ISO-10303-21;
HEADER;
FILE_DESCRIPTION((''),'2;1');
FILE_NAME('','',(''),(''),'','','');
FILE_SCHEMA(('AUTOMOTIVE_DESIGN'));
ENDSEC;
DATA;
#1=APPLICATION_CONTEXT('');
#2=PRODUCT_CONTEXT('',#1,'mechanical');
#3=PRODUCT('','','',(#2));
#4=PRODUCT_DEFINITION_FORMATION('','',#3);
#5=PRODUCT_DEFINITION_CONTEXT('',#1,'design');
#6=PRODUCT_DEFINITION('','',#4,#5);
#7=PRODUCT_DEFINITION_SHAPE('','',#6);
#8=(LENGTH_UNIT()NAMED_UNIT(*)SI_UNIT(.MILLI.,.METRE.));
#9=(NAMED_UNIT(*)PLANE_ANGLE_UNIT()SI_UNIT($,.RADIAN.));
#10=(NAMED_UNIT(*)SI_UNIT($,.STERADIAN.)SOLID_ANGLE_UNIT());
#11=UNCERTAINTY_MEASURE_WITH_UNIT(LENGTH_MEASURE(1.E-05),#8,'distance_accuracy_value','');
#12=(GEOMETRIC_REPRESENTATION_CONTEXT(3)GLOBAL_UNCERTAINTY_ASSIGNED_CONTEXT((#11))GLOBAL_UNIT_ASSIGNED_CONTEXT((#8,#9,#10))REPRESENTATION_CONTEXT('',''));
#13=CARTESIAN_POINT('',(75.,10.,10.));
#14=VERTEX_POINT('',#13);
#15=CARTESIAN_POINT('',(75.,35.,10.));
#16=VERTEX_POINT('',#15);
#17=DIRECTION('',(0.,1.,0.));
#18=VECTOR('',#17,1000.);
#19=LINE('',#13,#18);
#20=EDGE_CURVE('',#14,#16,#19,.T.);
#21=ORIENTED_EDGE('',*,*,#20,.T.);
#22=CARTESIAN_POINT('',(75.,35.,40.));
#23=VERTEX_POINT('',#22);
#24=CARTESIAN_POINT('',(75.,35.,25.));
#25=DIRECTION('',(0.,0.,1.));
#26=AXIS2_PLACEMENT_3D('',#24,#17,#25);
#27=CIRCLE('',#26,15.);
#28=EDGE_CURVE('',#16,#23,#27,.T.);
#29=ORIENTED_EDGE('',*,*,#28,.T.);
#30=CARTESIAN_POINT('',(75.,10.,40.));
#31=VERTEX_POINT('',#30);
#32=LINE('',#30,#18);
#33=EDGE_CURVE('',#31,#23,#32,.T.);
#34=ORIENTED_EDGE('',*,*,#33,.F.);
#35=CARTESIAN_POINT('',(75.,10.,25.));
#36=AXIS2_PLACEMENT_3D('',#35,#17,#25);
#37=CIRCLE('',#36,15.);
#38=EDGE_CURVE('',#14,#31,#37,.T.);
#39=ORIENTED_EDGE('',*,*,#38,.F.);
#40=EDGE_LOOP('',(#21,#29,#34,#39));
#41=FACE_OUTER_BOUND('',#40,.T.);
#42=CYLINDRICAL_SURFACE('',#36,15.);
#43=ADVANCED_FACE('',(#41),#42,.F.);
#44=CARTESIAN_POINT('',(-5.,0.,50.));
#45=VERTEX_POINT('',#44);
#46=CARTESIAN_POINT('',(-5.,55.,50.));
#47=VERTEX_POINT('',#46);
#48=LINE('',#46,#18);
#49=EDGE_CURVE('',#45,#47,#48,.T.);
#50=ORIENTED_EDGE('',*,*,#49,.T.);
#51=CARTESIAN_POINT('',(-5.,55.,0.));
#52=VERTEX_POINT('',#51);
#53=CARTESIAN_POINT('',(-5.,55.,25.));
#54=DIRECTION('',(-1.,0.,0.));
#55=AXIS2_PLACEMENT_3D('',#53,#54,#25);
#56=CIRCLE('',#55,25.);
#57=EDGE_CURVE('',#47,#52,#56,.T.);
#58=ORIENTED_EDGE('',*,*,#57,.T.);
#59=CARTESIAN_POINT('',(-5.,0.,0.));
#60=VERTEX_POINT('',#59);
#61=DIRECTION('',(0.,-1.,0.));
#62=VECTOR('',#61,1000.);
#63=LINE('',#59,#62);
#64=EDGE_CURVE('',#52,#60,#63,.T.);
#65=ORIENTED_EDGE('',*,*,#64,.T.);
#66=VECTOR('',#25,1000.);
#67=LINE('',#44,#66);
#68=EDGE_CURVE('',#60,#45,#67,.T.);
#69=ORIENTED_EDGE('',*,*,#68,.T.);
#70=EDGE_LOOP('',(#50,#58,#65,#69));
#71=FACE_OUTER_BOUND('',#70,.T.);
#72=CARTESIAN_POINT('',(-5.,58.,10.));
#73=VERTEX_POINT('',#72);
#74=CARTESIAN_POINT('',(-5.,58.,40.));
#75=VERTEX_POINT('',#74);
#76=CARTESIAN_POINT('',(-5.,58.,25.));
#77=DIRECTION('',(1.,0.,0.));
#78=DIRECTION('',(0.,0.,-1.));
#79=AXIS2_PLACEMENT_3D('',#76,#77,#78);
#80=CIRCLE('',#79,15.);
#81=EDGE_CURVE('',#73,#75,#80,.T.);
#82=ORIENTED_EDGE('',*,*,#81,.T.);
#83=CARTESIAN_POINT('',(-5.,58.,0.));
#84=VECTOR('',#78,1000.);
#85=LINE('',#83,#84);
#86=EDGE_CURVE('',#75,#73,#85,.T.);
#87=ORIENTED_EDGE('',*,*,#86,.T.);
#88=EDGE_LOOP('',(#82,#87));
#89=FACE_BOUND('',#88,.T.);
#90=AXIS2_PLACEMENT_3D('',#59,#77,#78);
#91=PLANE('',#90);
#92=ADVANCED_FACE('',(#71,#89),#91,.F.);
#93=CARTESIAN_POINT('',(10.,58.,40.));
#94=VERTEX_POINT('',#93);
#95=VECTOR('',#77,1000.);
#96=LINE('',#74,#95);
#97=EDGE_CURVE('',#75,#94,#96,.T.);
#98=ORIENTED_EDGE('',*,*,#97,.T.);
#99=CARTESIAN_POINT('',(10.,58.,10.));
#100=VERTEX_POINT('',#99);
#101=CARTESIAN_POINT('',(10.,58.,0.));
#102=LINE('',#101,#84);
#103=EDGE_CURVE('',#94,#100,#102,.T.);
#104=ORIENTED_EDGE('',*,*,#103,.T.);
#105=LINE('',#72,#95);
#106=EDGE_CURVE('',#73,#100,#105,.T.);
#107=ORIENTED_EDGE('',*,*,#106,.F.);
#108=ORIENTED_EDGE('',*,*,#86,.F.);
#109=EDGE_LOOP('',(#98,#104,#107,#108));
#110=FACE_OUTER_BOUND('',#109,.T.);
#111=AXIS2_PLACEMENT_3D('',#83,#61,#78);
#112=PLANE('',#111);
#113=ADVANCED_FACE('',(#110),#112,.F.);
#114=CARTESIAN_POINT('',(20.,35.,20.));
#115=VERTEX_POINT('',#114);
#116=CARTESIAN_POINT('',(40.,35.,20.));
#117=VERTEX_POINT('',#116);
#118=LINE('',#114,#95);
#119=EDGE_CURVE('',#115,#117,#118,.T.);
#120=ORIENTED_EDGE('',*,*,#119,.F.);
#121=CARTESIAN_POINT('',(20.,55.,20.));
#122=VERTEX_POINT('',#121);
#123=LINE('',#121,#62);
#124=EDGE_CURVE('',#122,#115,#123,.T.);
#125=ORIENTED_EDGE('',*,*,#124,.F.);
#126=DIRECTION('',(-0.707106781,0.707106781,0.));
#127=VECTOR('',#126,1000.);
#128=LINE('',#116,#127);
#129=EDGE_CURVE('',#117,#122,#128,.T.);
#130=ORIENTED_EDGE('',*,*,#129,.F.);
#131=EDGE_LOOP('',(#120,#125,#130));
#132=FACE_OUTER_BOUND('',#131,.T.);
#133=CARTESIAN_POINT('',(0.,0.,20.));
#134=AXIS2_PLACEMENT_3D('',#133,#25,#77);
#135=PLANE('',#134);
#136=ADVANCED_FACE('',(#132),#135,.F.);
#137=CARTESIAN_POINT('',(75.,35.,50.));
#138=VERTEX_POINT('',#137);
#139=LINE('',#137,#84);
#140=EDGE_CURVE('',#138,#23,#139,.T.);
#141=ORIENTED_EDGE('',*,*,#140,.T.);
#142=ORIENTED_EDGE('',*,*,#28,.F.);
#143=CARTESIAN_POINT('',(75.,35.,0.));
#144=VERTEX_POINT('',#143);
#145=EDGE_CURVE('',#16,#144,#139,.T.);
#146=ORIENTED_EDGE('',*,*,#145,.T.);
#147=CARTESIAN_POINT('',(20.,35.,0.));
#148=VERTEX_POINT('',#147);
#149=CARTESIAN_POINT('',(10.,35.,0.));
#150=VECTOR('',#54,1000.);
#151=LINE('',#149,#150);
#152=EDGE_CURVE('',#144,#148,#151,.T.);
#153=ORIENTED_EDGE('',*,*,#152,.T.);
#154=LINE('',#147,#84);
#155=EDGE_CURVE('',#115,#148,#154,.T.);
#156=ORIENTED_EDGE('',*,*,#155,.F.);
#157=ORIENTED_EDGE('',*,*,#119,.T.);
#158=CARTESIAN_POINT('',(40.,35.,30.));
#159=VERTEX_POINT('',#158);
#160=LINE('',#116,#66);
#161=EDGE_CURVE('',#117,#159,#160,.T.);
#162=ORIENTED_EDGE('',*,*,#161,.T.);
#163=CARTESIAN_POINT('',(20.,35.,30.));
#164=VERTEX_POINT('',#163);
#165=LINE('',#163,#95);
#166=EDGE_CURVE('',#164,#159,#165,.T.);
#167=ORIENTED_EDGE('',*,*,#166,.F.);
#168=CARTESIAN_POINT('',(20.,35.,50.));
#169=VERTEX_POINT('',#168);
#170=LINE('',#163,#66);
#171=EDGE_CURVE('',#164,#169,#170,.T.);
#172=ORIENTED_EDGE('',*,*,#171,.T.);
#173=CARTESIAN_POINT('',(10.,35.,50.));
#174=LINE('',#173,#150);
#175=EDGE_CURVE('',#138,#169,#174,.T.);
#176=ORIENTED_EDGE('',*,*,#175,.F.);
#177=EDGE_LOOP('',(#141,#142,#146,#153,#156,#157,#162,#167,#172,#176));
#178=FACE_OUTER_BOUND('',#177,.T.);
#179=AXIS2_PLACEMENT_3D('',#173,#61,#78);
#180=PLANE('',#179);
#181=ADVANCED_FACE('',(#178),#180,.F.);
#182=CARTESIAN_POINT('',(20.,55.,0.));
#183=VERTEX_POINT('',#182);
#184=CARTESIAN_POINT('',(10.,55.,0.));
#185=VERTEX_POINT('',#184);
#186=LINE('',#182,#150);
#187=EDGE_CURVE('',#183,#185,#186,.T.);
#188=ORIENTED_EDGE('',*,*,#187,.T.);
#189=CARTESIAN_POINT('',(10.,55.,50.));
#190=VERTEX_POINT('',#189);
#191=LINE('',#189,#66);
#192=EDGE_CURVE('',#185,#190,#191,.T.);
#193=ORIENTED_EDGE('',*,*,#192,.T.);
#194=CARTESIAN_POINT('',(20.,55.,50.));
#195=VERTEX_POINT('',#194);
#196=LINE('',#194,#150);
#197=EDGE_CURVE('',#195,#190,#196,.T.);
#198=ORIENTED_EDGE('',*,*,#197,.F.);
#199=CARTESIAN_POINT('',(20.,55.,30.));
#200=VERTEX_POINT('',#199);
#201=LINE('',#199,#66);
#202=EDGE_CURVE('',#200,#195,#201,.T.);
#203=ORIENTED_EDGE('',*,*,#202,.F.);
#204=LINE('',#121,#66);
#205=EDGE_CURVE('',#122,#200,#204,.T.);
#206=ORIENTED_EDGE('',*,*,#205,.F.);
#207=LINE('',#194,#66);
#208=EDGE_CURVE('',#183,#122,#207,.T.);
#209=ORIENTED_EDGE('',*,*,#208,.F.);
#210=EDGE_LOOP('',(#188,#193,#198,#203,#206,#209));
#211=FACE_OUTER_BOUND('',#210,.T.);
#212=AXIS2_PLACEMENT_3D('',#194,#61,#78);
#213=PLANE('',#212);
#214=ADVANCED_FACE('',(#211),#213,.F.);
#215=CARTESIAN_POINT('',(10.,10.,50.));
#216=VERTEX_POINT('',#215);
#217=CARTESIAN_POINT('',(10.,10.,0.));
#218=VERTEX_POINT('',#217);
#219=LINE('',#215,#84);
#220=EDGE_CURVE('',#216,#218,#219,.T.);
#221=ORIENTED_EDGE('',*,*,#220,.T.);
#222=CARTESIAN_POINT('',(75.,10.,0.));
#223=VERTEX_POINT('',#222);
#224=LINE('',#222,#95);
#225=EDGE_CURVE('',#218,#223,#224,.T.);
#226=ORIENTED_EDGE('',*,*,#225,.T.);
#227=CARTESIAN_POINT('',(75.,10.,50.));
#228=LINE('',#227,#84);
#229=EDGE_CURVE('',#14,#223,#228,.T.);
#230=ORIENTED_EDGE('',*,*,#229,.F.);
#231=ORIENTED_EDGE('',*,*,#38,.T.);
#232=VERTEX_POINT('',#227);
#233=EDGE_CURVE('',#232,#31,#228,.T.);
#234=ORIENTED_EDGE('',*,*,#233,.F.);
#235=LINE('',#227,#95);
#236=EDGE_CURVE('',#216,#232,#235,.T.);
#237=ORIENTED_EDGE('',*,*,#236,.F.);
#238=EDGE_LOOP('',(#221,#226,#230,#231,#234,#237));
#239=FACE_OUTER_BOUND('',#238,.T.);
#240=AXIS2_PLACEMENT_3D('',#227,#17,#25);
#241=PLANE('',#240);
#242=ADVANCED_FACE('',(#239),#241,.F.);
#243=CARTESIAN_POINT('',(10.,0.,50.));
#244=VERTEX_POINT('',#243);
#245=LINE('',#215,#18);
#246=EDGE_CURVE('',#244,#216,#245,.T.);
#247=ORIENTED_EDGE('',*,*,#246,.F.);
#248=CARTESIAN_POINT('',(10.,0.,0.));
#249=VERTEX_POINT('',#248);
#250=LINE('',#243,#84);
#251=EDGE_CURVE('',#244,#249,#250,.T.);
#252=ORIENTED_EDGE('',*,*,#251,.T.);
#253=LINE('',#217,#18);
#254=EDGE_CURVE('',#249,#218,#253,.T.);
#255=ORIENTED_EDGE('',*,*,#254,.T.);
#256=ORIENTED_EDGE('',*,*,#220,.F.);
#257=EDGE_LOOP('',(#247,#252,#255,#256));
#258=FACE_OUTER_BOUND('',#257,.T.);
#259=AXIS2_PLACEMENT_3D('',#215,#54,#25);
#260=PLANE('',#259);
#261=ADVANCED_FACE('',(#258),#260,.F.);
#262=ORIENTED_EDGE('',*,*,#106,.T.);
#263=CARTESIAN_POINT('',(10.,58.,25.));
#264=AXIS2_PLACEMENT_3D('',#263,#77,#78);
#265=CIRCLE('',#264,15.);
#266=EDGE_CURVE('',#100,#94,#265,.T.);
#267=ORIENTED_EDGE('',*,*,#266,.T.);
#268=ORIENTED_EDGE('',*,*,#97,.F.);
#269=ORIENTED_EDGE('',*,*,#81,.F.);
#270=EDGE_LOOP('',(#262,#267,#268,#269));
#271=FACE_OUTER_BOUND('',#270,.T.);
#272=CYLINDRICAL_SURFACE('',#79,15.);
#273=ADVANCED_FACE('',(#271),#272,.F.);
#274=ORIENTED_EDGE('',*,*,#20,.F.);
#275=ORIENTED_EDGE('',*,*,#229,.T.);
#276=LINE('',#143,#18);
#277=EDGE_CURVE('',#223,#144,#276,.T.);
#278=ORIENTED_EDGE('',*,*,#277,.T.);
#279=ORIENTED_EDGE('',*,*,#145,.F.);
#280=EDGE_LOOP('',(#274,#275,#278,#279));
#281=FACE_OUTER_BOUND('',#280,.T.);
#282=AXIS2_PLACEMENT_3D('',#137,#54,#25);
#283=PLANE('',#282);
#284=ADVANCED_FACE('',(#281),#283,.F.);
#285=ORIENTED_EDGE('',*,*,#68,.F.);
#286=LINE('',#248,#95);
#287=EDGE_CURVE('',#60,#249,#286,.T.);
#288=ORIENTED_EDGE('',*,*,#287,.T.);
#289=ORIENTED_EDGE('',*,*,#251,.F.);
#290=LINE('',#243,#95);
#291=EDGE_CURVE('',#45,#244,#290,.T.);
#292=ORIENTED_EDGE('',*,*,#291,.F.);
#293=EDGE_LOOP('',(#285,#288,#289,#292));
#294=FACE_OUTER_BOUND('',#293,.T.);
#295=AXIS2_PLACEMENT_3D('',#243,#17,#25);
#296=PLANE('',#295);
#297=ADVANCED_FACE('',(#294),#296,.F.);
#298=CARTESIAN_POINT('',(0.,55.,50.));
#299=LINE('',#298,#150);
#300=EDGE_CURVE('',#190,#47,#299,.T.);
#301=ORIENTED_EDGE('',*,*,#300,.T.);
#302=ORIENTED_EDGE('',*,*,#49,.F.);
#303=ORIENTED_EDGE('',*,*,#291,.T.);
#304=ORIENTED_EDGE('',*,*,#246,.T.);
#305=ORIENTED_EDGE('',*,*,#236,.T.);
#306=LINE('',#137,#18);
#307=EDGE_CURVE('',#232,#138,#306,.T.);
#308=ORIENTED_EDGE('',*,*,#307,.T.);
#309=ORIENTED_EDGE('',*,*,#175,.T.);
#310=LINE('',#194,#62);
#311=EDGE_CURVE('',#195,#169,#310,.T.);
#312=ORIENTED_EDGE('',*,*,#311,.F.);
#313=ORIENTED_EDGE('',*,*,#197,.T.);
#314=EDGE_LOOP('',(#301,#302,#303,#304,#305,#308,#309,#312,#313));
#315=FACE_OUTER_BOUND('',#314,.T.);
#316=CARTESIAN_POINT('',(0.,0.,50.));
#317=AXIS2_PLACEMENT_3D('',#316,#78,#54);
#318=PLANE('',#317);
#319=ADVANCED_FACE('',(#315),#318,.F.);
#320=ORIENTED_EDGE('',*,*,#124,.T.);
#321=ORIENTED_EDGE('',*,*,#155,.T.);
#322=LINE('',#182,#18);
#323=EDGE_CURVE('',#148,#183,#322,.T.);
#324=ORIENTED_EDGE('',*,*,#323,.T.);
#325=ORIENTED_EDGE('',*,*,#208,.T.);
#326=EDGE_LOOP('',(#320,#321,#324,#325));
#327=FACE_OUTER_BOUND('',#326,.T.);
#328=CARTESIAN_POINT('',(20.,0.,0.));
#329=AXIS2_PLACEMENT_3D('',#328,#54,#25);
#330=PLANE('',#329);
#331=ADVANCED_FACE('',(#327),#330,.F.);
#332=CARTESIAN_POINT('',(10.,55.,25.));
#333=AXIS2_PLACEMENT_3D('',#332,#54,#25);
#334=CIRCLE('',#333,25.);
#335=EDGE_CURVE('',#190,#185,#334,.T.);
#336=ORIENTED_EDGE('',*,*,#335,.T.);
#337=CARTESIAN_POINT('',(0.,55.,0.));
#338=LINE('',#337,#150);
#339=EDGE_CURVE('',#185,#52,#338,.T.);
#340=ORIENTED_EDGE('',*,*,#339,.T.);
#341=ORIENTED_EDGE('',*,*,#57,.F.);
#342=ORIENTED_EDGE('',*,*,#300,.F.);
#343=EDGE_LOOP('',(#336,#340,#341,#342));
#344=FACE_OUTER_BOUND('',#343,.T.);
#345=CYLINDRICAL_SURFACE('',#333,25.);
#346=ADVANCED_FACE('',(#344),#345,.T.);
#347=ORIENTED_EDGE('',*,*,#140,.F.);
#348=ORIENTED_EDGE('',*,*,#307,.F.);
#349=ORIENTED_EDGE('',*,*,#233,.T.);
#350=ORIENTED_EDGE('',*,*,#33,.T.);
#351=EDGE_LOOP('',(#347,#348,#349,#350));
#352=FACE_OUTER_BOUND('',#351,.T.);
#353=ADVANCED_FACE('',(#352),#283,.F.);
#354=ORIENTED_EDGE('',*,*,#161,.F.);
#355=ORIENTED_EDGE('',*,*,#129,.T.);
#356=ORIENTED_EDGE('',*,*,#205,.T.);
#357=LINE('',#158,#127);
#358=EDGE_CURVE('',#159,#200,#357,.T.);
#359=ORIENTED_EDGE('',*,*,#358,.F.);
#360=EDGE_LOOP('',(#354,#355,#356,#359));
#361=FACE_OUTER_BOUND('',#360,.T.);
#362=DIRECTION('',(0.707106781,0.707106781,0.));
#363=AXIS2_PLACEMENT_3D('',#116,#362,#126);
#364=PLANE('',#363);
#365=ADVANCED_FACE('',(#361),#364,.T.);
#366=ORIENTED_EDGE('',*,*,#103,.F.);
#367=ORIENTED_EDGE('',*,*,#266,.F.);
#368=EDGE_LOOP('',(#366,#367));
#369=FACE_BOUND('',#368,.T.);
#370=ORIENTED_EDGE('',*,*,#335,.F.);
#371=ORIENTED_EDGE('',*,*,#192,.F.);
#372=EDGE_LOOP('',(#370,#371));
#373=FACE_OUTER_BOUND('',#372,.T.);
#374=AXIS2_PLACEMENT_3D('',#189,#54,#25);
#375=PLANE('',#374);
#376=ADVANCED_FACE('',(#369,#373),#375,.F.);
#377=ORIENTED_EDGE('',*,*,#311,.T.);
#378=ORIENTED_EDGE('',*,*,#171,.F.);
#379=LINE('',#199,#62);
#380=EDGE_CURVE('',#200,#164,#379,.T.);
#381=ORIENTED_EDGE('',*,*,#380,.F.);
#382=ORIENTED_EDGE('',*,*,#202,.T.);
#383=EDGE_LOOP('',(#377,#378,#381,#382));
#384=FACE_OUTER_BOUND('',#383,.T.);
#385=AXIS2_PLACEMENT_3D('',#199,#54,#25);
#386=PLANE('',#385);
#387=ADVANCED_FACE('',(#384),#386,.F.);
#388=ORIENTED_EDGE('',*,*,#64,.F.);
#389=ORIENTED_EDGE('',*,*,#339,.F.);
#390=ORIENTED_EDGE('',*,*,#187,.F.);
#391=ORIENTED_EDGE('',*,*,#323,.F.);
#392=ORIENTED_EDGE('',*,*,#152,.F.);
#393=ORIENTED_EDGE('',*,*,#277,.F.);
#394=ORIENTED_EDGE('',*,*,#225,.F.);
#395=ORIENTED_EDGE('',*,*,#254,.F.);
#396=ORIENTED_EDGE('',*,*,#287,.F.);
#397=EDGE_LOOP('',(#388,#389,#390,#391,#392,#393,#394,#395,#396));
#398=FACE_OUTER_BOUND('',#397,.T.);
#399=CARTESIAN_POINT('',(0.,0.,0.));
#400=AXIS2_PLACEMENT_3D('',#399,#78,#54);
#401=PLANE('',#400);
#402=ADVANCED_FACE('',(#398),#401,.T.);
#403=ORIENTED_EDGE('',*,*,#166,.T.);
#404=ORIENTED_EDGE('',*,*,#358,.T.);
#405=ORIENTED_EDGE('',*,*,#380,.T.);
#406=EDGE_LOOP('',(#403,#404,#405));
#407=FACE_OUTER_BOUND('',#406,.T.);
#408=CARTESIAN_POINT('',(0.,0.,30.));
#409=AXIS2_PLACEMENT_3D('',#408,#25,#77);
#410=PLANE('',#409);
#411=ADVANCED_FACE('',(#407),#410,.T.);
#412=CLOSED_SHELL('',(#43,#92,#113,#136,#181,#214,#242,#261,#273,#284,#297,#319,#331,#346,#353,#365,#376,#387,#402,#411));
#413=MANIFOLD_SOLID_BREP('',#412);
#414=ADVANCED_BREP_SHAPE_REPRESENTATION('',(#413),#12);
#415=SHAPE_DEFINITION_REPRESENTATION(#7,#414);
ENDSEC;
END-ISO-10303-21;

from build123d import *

# Parameters (mm, degrees)
BASE_BLOCK_50MM_DEPTH         = 50
STEP_BOSS_SKETCH_W            = 50
STEP_BOSS_SKETCH_H            = 55
STEP_BOSS_10MM_DEPTH          = 10
STEP_CUT_SKETCH_W             = 50
STEP_CUT_SKETCH_H             = 55
STEP_CUT_10MM_DEPTH           = 10
UPRIGHT_PAD_SKETCH_W          = 50
UPRIGHT_PAD_SKETCH_H          = 55
UPRIGHT_PAD_5MM_DEPTH         = 5
ARCH_BOSS_15MM_DEPTH          = 15
UPPER_BLOCK_SKETCH_W          = 50
UPPER_BLOCK_SKETCH_H          = 20
UPPER_BLOCK_10MM_DEPTH        = 10
BASE_SEMICIRCULAR_NOTCH_DEPTH = 15
ARCH_SEMICIRCULAR_CUT_DEPTH   = 25
SUPPORT_RIB_30MM_DEPTH        = 30
RIB_TRIM_CUT_20MM_DEPTH       = 20


with BuildPart() as part:
    # Base Profile Sketch → Base Block 50mm (new body)
    with BuildSketch(Plane.XY):
        Polygon((0, 0), (0, 55), (10, 55), (10, 35), (75, 35), (75, 10), (10, 10), (10, 0), align=None)
    extrude(amount=BASE_BLOCK_50MM_DEPTH)

    # Step Boss Sketch → Step Boss 10mm (add)
    with BuildSketch(Plane.ZY):
        with Locations((25, 27.5)):
            Rectangle(STEP_BOSS_SKETCH_W, STEP_BOSS_SKETCH_H)
    extrude(amount=STEP_BOSS_10MM_DEPTH)

    # Step Cut Sketch → Step Cut 10mm (cut)
    with BuildSketch(Plane.ZY.offset(10)):
        with Locations((25, 27.5)):
            Rectangle(STEP_CUT_SKETCH_W, STEP_CUT_SKETCH_H)
    extrude(amount=-STEP_CUT_10MM_DEPTH, mode=Mode.SUBTRACT)

    # Upright Pad Sketch → Upright Pad 5mm (add)
    with BuildSketch(Plane.ZY):
        with Locations((25, 27.5)):
            Rectangle(UPRIGHT_PAD_SKETCH_W, UPRIGHT_PAD_SKETCH_H)
    extrude(amount=UPRIGHT_PAD_5MM_DEPTH)

    # Arch Boss Sketch R25 → Arch Boss 15mm (add)
    with BuildSketch(Plane.ZY.offset(5)):
        with BuildLine():
            Line((0, 55), (50, 55))
            ThreePointArc((50, 55), (25, 80), (0, 55))
        make_face()
    extrude(amount=-ARCH_BOSS_15MM_DEPTH)

    # Upper Block Sketch → Upper Block 10mm (add)
    with BuildSketch(Plane(origin=(10, 0, 0), x_dir=(0, 0, -1), z_dir=(1, 0, 0))):
        with Locations((-25, 45)):
            Rectangle(UPPER_BLOCK_SKETCH_W, UPPER_BLOCK_SKETCH_H)
    extrude(amount=UPPER_BLOCK_10MM_DEPTH)

    # Base Notch Sketch Ø30 → Base Semicircular Notch (cut)
    with BuildSketch(Plane(origin=(10, 0, 0), x_dir=(0, 0, -1), z_dir=(1, 0, 0))):
        with BuildLine():
            Line((-40, 58), (-25, 58))
            Line((-25, 58), (-10, 58))
            ThreePointArc((-10, 58), (-25, 73), (-40, 58))
        make_face()
    extrude(amount=-BASE_SEMICIRCULAR_NOTCH_DEPTH, mode=Mode.SUBTRACT)

    # Arch Cut Sketch Ø30 → Arch Semicircular Cut (cut)
    with BuildSketch(Plane(origin=(0, 35, 0), x_dir=(1, 0, 0), z_dir=(0, 1, 0))):
        with BuildLine():
            Line((75, -10), (75, -40))
            ThreePointArc((75, -40), (60, -25), (75, -10))
        make_face()
    extrude(amount=-ARCH_SEMICIRCULAR_CUT_DEPTH, mode=Mode.SUBTRACT)

    # Rib Sketch → Support Rib 30mm (add)
    with BuildSketch(Plane.XY.offset(50)):
        Polygon((20, 55), (20, 35), (40, 35), align=None)
    extrude(amount=-SUPPORT_RIB_30MM_DEPTH)

    # Rib Trim Sketch → Rib Trim Cut 20mm (cut)
    with BuildSketch(Plane.XY.offset(50)):
        Polygon((20, 55), (20, 35), (40, 35), align=None)
    extrude(amount=-RIB_TRIM_CUT_20MM_DEPTH, mode=Mode.SUBTRACT)


solid = part.part
